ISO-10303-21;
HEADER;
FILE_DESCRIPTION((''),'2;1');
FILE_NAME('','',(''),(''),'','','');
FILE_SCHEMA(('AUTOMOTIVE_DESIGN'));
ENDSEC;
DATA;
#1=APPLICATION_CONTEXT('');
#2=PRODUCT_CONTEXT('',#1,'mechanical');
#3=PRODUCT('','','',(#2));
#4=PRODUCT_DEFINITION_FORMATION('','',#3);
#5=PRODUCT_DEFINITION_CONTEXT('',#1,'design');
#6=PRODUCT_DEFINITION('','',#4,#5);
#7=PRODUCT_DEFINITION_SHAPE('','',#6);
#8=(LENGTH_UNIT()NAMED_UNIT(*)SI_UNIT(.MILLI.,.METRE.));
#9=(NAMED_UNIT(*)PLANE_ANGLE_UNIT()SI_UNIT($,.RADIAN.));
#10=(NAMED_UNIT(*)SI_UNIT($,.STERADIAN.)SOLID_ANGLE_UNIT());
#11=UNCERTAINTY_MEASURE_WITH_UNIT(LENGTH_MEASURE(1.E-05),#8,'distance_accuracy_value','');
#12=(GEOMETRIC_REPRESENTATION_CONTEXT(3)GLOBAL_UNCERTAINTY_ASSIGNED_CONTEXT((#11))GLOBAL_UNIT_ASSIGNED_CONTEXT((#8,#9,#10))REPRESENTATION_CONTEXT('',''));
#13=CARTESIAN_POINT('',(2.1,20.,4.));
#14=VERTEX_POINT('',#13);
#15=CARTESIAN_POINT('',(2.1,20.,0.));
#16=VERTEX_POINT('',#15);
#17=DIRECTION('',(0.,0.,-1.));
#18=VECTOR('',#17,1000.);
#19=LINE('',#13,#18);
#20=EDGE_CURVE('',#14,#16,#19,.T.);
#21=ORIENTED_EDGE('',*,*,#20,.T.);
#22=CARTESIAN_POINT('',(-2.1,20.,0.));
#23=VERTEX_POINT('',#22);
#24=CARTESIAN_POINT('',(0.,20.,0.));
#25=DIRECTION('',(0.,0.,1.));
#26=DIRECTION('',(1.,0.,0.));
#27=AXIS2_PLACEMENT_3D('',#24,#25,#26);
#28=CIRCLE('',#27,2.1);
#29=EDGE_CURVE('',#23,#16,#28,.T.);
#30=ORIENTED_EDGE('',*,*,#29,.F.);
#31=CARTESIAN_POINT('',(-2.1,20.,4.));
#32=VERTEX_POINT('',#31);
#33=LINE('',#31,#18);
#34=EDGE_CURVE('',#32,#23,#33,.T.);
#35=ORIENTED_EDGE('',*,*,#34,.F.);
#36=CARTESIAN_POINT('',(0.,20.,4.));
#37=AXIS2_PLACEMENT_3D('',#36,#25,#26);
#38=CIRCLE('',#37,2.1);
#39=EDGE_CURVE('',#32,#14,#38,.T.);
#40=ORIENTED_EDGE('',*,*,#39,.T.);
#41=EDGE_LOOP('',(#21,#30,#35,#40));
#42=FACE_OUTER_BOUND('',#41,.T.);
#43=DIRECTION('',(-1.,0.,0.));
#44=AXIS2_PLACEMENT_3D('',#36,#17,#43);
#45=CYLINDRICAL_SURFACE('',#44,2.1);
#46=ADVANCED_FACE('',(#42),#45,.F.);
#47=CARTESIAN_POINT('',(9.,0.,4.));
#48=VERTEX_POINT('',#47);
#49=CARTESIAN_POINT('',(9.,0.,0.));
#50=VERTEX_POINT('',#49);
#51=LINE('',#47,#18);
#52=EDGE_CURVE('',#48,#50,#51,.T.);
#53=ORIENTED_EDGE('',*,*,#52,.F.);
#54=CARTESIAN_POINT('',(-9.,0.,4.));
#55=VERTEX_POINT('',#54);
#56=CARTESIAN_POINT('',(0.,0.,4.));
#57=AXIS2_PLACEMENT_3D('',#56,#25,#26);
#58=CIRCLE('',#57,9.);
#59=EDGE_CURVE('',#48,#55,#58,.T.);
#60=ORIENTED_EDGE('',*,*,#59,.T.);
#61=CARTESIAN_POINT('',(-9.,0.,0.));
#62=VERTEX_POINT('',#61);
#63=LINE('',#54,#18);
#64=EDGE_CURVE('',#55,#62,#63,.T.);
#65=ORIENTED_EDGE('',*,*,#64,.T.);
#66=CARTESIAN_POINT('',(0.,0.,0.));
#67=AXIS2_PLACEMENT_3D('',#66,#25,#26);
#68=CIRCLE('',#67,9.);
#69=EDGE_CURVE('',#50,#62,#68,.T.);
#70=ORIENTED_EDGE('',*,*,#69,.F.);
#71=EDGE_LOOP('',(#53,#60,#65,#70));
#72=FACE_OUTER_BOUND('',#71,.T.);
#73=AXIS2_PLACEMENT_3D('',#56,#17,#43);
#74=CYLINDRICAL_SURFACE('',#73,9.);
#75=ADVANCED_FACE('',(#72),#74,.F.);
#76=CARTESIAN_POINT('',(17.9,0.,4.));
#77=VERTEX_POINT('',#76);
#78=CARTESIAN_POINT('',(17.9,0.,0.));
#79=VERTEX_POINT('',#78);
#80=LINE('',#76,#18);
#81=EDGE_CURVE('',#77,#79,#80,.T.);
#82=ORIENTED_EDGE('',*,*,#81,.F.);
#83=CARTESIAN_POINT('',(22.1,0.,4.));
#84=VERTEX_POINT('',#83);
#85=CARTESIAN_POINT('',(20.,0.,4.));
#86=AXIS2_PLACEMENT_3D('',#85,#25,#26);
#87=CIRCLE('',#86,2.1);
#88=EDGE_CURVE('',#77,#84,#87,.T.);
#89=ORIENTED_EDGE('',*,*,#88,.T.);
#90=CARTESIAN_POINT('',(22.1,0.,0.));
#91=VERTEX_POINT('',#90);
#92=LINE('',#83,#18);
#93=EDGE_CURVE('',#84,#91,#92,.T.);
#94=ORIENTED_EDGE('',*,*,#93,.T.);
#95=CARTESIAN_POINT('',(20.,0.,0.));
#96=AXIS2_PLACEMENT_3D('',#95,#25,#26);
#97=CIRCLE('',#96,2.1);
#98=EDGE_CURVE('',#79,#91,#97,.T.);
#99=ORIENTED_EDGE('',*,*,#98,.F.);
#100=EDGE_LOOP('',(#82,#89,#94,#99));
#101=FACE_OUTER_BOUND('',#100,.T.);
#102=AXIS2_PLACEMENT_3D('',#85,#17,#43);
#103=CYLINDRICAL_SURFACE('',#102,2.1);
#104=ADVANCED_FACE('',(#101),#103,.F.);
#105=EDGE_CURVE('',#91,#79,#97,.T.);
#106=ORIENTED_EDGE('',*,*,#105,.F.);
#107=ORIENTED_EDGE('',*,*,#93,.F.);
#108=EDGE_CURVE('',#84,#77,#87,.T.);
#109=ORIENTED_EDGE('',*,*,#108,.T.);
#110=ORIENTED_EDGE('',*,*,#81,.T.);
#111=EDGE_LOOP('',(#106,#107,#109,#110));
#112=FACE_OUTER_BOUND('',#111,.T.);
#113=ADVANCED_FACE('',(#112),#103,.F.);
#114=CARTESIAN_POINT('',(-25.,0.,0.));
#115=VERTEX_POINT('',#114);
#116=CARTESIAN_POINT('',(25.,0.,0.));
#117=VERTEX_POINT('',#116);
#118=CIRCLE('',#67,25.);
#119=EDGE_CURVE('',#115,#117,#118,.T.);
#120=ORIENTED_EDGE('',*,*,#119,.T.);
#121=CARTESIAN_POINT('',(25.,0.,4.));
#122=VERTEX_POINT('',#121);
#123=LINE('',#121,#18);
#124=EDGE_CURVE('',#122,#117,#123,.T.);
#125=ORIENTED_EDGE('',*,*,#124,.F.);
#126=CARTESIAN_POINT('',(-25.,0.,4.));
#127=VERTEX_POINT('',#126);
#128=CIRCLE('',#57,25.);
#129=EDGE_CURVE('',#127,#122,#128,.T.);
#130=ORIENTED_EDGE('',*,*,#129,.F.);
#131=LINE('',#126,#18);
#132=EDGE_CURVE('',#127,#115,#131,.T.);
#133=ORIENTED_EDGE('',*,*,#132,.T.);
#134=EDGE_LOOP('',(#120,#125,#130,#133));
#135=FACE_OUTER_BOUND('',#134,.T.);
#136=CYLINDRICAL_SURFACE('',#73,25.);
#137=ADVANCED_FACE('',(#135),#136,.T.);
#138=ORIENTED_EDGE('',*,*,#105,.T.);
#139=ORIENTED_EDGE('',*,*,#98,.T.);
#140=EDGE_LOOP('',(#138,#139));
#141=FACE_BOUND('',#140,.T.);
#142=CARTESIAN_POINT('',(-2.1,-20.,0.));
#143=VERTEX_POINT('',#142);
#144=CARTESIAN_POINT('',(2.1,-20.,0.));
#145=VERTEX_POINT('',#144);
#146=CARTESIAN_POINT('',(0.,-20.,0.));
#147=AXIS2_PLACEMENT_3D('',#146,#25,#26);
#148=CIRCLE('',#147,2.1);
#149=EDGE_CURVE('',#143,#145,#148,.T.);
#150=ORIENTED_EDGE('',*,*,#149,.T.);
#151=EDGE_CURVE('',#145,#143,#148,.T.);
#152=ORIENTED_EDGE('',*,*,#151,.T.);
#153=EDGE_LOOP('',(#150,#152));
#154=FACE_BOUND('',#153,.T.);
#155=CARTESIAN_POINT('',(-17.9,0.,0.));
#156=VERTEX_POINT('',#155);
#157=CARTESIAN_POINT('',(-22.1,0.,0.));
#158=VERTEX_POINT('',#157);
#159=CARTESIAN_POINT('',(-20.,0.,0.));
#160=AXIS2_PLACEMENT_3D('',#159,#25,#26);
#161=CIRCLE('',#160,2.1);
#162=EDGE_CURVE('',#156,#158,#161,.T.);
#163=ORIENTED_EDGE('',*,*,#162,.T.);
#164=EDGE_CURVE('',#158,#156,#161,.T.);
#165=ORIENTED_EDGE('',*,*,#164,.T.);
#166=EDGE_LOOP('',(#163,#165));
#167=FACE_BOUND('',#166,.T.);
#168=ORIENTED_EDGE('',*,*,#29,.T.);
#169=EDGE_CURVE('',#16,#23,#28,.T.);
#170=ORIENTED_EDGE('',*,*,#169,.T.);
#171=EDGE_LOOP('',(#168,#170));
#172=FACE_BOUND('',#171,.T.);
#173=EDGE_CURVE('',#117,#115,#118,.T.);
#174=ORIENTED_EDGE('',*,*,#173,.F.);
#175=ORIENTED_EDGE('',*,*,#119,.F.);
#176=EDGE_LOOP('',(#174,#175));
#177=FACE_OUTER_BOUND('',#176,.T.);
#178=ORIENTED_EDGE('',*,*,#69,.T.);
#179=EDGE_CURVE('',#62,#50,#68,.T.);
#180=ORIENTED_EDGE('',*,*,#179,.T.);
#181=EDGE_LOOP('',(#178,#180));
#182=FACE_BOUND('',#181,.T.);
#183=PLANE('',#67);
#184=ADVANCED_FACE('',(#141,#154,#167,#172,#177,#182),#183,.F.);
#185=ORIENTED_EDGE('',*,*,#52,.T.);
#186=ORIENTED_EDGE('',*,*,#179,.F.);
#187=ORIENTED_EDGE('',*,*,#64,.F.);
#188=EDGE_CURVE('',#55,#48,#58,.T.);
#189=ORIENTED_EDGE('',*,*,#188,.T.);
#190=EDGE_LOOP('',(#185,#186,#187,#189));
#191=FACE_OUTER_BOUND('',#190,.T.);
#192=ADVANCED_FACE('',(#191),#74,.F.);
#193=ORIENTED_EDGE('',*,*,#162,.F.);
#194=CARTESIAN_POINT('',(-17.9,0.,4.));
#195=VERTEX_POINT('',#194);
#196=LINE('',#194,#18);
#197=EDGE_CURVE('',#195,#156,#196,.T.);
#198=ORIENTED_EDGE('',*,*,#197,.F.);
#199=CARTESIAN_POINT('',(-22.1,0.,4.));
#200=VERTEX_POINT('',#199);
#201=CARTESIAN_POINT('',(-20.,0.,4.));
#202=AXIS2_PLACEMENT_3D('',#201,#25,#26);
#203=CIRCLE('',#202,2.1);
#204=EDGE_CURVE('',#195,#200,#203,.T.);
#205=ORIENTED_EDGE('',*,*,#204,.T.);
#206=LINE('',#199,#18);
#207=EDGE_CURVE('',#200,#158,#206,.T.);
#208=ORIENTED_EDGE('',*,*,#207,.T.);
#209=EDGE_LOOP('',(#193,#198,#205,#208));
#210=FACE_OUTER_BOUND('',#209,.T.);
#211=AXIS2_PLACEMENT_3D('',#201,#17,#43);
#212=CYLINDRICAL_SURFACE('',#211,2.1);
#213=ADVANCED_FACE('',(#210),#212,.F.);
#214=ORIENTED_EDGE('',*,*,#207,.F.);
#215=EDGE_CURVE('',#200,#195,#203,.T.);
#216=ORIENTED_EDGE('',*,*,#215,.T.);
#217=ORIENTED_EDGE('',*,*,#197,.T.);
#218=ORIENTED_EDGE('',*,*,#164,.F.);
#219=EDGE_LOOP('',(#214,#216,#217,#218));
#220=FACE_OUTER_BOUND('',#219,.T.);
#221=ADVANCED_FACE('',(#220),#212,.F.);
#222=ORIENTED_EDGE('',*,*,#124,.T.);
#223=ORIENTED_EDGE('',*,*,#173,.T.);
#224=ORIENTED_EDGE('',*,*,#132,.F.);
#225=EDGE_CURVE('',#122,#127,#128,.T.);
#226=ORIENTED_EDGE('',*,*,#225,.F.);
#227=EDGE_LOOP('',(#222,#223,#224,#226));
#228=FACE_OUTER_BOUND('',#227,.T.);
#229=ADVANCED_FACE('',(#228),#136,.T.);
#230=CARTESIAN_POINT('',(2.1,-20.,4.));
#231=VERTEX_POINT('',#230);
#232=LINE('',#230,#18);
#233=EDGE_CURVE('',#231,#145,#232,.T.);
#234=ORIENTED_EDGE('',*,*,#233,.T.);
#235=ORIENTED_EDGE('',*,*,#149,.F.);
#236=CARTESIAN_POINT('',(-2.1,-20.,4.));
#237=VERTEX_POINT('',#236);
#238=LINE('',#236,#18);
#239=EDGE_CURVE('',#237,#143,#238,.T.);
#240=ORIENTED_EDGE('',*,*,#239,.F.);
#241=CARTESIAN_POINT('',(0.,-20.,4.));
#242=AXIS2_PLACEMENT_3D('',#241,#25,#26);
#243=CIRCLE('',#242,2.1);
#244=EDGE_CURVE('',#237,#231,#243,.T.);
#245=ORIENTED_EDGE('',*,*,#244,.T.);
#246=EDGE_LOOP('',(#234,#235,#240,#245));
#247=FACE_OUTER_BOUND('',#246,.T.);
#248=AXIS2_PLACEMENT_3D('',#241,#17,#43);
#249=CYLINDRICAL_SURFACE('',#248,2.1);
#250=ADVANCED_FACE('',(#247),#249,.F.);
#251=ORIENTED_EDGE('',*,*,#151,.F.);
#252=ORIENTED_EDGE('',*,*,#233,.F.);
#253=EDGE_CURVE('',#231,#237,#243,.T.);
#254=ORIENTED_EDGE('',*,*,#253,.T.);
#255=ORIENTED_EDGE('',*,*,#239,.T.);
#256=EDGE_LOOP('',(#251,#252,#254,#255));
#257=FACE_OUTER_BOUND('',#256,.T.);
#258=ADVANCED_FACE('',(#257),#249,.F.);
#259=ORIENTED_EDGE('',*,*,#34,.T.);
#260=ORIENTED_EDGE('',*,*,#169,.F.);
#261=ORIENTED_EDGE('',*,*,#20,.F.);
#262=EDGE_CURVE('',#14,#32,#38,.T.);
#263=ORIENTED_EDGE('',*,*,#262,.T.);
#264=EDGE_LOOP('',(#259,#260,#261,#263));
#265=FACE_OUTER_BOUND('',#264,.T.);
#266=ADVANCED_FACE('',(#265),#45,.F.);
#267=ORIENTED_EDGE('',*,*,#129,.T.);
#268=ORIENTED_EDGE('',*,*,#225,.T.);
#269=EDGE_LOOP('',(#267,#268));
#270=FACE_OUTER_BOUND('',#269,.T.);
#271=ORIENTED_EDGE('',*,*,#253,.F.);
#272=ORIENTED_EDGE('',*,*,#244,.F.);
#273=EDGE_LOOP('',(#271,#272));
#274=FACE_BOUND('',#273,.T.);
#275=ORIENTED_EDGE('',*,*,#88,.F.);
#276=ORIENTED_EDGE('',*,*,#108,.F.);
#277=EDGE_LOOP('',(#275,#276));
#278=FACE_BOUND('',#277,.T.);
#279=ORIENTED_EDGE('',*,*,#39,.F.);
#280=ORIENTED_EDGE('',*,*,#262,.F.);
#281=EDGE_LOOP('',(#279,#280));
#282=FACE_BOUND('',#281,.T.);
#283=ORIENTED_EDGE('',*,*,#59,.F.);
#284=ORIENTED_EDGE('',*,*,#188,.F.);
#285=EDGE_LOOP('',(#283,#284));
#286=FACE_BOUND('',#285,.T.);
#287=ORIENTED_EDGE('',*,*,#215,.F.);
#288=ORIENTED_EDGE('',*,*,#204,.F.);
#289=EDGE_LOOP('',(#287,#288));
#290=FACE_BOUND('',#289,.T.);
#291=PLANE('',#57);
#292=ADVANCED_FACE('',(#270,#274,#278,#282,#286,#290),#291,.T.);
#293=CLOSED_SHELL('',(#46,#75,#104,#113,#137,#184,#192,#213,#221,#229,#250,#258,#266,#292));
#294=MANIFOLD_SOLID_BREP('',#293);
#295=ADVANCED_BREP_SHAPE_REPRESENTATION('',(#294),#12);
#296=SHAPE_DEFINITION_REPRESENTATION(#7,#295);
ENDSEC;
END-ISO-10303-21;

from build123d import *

# Parameters (mm, degrees)
SKETCH1_R           = 25
SKETCH1_R_2         = 9
SKETCH1_R_3         = 2.1
BOSS_EXTRUDE1_DEPTH = 4


with BuildPart() as part:
    # Sketch1 → Boss-Extrude1 (new body)
    with BuildSketch(Plane.XY):
        Circle(SKETCH1_R)
        Circle(SKETCH1_R_2, mode=Mode.SUBTRACT)
        with Locations((0, 20)):
            Circle(SKETCH1_R_3, mode=Mode.SUBTRACT)
        with Locations((-20, 0)):
            Circle(SKETCH1_R_3, mode=Mode.SUBTRACT)
        with Locations((20, 0)):
            Circle(SKETCH1_R_3, mode=Mode.SUBTRACT)
        with Locations((0, -20)):
            Circle(SKETCH1_R_3, mode=Mode.SUBTRACT)
    extrude(amount=BOSS_EXTRUDE1_DEPTH)


solid = part.part
